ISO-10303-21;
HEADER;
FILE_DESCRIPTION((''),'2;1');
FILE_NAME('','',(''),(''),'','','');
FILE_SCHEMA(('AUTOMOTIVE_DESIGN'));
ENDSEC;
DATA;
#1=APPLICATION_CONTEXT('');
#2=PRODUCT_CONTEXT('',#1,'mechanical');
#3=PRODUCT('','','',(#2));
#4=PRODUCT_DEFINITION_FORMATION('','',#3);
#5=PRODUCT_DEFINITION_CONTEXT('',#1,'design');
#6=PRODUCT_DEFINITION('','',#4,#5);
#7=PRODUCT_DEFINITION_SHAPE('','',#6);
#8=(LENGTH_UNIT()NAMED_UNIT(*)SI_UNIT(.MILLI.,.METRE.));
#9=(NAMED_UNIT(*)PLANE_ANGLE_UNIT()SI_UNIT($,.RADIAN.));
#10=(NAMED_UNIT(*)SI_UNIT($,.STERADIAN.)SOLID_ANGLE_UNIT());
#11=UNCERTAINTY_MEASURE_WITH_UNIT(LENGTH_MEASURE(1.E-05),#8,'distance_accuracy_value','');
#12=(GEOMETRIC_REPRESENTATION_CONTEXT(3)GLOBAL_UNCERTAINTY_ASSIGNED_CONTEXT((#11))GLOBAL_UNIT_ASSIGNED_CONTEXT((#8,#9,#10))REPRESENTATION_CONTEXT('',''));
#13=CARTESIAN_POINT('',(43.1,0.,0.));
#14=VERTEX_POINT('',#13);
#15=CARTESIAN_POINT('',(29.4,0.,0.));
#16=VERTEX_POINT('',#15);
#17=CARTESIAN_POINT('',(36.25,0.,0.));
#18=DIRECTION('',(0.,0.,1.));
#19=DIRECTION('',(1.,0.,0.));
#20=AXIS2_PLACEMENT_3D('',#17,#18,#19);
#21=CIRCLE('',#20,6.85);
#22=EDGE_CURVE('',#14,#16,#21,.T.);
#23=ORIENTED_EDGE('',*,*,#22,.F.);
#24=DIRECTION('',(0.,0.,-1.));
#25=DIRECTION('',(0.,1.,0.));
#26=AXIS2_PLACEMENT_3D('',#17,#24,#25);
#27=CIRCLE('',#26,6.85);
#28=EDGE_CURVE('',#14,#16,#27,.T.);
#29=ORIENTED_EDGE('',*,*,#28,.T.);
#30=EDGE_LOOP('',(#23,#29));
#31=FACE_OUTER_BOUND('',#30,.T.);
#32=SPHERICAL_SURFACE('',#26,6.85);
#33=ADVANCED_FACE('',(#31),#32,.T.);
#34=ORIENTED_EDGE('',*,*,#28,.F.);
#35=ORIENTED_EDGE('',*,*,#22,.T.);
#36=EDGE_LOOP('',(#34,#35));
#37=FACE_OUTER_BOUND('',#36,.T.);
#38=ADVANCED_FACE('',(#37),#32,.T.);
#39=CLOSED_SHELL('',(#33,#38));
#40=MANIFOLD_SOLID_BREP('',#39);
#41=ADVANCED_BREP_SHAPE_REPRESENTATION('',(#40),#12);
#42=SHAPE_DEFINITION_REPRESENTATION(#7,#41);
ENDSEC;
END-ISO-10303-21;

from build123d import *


with BuildPart() as part:
    # Sketch1 → Revolve1 (revolve)
    with BuildSketch(Plane.XY):
        with BuildLine():
            Line((29.4, 0), (43.1, 0))
            ThreePointArc((43.1, 0), (36.25, 6.85), (29.4, 0))
        make_face()
    revolve(axis=Axis((0, 0, 0), (1, 0, 0)))


solid = part.part
